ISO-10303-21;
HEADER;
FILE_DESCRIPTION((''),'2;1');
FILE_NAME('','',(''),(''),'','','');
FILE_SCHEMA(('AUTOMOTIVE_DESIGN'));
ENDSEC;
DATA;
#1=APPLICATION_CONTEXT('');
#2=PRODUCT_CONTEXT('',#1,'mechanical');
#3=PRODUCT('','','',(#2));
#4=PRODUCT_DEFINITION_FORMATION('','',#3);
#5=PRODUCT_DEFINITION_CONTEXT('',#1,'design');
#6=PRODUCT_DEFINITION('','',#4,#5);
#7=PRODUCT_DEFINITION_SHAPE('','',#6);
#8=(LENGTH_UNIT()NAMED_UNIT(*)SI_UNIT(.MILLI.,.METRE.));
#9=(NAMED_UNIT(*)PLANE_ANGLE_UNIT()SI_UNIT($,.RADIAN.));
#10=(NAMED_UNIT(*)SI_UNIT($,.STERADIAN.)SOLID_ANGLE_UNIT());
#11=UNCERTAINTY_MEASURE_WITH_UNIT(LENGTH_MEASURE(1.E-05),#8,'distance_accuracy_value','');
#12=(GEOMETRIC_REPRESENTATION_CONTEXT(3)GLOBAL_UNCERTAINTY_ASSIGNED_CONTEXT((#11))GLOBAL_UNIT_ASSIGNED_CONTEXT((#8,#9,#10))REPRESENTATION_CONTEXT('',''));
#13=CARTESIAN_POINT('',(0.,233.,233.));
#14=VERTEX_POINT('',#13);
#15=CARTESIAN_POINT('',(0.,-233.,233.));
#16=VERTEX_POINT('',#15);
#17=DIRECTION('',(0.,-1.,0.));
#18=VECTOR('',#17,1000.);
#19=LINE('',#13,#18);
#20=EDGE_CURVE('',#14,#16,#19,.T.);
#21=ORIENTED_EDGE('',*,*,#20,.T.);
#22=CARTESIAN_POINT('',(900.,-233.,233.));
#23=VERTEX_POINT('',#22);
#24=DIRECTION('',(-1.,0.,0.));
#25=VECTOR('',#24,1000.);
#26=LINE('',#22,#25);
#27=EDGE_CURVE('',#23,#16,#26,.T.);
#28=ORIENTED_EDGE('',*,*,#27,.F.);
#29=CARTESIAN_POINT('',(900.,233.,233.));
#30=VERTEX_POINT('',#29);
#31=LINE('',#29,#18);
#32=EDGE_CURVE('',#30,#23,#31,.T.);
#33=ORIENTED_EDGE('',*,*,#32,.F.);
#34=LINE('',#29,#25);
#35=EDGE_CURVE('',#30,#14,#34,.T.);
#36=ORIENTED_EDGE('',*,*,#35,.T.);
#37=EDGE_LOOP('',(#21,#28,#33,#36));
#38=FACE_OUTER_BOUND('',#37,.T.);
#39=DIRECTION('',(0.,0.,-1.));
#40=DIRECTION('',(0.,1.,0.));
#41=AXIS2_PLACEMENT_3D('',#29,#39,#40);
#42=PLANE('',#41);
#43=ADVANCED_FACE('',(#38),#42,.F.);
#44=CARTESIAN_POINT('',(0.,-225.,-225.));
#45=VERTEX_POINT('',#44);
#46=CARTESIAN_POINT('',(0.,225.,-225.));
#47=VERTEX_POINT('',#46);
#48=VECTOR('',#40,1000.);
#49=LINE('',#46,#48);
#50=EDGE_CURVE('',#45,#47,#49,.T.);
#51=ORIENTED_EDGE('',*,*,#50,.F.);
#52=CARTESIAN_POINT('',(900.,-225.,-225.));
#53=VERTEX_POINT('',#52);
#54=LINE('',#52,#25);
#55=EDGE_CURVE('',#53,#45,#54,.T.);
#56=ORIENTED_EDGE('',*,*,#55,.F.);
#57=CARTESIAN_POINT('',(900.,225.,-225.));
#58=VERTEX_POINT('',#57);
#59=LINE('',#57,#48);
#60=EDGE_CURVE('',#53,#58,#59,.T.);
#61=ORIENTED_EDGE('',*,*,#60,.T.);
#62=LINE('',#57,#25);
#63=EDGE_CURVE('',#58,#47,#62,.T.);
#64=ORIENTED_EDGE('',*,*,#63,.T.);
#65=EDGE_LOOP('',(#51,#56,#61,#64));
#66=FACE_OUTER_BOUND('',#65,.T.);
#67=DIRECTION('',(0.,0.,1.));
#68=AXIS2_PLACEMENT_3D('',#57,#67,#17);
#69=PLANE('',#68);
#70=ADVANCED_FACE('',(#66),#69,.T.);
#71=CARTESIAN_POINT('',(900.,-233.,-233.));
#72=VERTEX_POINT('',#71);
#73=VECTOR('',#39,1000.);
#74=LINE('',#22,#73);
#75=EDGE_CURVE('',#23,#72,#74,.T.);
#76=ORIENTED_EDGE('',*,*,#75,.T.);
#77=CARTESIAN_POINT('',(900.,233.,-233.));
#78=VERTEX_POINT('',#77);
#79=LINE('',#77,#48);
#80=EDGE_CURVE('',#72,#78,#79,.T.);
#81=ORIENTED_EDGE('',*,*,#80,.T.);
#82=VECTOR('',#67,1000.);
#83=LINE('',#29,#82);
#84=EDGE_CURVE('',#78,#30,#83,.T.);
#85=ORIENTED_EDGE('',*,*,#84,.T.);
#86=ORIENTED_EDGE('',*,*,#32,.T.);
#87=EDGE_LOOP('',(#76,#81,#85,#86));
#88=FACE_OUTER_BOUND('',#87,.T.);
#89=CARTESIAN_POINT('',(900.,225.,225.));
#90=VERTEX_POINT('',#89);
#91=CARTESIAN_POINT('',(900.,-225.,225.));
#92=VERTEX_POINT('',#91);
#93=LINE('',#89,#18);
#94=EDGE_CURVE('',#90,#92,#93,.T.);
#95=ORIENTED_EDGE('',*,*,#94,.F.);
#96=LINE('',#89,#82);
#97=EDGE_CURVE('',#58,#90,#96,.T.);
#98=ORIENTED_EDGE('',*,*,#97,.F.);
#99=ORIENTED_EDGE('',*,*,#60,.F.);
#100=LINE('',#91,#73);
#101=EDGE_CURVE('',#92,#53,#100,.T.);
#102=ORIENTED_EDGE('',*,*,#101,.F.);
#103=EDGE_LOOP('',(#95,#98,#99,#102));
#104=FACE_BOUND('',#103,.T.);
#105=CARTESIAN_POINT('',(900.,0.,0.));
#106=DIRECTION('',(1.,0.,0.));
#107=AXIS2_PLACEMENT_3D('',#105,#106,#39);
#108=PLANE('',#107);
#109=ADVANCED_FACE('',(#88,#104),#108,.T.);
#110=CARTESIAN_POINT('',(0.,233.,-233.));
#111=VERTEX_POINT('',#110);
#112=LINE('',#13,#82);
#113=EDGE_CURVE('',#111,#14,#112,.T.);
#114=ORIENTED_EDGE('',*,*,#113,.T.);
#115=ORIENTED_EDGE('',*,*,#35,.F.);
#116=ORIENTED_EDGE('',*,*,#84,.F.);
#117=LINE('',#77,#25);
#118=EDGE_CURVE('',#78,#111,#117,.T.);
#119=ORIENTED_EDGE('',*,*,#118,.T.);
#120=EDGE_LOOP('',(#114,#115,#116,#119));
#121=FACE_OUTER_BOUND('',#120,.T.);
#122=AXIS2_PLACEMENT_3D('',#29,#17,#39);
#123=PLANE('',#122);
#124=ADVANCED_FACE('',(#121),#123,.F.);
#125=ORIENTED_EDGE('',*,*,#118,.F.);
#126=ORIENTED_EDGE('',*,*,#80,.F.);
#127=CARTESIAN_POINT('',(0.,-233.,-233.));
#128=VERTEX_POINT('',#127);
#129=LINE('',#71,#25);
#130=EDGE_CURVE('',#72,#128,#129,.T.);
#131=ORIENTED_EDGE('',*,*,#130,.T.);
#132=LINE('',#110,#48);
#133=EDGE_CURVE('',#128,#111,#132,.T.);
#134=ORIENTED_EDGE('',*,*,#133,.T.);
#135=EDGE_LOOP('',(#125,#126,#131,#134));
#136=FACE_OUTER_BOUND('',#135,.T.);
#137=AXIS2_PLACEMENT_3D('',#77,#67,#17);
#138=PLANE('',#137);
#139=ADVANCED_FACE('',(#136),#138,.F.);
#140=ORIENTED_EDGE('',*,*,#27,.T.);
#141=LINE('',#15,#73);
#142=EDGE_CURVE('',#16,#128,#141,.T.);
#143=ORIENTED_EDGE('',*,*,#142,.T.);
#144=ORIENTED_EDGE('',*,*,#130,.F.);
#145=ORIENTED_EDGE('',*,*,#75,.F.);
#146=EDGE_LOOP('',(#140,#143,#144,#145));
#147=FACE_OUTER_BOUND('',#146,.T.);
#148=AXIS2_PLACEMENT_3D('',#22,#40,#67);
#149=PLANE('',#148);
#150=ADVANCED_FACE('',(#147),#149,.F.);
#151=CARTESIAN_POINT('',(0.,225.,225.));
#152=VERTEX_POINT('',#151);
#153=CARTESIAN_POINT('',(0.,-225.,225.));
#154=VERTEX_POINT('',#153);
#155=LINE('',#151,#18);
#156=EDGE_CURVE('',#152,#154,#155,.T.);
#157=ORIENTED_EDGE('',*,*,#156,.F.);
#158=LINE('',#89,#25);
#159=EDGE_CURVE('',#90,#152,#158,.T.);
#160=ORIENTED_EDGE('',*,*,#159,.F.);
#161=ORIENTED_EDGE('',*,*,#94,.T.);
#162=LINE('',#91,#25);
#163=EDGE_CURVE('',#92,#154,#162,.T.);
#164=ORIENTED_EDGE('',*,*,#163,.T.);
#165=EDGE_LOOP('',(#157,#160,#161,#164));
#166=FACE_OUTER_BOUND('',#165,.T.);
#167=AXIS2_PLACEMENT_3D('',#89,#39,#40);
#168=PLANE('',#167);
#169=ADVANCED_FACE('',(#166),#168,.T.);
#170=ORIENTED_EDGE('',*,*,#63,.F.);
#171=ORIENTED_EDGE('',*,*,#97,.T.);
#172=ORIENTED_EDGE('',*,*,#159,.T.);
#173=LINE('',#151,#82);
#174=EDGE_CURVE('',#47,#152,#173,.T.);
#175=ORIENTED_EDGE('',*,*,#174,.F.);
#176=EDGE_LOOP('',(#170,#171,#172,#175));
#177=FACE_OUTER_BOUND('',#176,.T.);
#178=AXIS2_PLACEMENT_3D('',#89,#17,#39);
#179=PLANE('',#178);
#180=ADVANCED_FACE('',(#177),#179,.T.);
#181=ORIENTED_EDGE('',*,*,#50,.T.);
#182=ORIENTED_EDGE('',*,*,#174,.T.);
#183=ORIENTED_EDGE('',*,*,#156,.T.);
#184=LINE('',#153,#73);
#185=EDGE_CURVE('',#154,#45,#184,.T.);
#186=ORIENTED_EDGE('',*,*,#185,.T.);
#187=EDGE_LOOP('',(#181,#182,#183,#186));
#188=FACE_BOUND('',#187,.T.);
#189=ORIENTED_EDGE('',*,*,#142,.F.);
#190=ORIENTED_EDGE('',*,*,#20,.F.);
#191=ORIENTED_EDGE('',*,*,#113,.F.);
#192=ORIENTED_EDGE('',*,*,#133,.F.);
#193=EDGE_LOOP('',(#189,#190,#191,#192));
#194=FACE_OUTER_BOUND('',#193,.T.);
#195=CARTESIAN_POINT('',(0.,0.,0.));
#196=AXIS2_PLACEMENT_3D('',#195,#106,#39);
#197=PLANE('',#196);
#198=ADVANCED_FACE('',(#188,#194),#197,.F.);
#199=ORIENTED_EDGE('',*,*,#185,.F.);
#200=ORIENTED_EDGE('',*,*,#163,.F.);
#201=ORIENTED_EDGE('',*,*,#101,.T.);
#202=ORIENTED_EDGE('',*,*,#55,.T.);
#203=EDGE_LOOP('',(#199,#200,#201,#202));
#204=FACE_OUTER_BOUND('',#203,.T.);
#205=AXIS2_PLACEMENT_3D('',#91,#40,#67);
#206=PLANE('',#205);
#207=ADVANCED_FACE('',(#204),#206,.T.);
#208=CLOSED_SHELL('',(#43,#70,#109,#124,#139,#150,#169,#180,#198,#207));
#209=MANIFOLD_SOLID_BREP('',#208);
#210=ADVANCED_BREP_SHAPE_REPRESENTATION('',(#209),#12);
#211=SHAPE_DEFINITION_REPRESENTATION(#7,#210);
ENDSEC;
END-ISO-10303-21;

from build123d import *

# Parameters (mm, degrees)
SKETCH1_W           = 466
SKETCH1_H           = 466
SKETCH1_W_2         = 450
SKETCH1_H_2         = 450
BOSS_EXTRUDE1_DEPTH = 900


with BuildPart() as part:
    # Sketch1 → Boss-Extrude1 (new body)
    with BuildSketch(Plane(origin=(0, 0, 0), x_dir=(0, 0, -1), z_dir=(1, 0, 0))):
        Rectangle(SKETCH1_W, SKETCH1_H)
        Rectangle(SKETCH1_W_2, SKETCH1_H_2, mode=Mode.SUBTRACT)
    extrude(amount=BOSS_EXTRUDE1_DEPTH)


solid = part.part
